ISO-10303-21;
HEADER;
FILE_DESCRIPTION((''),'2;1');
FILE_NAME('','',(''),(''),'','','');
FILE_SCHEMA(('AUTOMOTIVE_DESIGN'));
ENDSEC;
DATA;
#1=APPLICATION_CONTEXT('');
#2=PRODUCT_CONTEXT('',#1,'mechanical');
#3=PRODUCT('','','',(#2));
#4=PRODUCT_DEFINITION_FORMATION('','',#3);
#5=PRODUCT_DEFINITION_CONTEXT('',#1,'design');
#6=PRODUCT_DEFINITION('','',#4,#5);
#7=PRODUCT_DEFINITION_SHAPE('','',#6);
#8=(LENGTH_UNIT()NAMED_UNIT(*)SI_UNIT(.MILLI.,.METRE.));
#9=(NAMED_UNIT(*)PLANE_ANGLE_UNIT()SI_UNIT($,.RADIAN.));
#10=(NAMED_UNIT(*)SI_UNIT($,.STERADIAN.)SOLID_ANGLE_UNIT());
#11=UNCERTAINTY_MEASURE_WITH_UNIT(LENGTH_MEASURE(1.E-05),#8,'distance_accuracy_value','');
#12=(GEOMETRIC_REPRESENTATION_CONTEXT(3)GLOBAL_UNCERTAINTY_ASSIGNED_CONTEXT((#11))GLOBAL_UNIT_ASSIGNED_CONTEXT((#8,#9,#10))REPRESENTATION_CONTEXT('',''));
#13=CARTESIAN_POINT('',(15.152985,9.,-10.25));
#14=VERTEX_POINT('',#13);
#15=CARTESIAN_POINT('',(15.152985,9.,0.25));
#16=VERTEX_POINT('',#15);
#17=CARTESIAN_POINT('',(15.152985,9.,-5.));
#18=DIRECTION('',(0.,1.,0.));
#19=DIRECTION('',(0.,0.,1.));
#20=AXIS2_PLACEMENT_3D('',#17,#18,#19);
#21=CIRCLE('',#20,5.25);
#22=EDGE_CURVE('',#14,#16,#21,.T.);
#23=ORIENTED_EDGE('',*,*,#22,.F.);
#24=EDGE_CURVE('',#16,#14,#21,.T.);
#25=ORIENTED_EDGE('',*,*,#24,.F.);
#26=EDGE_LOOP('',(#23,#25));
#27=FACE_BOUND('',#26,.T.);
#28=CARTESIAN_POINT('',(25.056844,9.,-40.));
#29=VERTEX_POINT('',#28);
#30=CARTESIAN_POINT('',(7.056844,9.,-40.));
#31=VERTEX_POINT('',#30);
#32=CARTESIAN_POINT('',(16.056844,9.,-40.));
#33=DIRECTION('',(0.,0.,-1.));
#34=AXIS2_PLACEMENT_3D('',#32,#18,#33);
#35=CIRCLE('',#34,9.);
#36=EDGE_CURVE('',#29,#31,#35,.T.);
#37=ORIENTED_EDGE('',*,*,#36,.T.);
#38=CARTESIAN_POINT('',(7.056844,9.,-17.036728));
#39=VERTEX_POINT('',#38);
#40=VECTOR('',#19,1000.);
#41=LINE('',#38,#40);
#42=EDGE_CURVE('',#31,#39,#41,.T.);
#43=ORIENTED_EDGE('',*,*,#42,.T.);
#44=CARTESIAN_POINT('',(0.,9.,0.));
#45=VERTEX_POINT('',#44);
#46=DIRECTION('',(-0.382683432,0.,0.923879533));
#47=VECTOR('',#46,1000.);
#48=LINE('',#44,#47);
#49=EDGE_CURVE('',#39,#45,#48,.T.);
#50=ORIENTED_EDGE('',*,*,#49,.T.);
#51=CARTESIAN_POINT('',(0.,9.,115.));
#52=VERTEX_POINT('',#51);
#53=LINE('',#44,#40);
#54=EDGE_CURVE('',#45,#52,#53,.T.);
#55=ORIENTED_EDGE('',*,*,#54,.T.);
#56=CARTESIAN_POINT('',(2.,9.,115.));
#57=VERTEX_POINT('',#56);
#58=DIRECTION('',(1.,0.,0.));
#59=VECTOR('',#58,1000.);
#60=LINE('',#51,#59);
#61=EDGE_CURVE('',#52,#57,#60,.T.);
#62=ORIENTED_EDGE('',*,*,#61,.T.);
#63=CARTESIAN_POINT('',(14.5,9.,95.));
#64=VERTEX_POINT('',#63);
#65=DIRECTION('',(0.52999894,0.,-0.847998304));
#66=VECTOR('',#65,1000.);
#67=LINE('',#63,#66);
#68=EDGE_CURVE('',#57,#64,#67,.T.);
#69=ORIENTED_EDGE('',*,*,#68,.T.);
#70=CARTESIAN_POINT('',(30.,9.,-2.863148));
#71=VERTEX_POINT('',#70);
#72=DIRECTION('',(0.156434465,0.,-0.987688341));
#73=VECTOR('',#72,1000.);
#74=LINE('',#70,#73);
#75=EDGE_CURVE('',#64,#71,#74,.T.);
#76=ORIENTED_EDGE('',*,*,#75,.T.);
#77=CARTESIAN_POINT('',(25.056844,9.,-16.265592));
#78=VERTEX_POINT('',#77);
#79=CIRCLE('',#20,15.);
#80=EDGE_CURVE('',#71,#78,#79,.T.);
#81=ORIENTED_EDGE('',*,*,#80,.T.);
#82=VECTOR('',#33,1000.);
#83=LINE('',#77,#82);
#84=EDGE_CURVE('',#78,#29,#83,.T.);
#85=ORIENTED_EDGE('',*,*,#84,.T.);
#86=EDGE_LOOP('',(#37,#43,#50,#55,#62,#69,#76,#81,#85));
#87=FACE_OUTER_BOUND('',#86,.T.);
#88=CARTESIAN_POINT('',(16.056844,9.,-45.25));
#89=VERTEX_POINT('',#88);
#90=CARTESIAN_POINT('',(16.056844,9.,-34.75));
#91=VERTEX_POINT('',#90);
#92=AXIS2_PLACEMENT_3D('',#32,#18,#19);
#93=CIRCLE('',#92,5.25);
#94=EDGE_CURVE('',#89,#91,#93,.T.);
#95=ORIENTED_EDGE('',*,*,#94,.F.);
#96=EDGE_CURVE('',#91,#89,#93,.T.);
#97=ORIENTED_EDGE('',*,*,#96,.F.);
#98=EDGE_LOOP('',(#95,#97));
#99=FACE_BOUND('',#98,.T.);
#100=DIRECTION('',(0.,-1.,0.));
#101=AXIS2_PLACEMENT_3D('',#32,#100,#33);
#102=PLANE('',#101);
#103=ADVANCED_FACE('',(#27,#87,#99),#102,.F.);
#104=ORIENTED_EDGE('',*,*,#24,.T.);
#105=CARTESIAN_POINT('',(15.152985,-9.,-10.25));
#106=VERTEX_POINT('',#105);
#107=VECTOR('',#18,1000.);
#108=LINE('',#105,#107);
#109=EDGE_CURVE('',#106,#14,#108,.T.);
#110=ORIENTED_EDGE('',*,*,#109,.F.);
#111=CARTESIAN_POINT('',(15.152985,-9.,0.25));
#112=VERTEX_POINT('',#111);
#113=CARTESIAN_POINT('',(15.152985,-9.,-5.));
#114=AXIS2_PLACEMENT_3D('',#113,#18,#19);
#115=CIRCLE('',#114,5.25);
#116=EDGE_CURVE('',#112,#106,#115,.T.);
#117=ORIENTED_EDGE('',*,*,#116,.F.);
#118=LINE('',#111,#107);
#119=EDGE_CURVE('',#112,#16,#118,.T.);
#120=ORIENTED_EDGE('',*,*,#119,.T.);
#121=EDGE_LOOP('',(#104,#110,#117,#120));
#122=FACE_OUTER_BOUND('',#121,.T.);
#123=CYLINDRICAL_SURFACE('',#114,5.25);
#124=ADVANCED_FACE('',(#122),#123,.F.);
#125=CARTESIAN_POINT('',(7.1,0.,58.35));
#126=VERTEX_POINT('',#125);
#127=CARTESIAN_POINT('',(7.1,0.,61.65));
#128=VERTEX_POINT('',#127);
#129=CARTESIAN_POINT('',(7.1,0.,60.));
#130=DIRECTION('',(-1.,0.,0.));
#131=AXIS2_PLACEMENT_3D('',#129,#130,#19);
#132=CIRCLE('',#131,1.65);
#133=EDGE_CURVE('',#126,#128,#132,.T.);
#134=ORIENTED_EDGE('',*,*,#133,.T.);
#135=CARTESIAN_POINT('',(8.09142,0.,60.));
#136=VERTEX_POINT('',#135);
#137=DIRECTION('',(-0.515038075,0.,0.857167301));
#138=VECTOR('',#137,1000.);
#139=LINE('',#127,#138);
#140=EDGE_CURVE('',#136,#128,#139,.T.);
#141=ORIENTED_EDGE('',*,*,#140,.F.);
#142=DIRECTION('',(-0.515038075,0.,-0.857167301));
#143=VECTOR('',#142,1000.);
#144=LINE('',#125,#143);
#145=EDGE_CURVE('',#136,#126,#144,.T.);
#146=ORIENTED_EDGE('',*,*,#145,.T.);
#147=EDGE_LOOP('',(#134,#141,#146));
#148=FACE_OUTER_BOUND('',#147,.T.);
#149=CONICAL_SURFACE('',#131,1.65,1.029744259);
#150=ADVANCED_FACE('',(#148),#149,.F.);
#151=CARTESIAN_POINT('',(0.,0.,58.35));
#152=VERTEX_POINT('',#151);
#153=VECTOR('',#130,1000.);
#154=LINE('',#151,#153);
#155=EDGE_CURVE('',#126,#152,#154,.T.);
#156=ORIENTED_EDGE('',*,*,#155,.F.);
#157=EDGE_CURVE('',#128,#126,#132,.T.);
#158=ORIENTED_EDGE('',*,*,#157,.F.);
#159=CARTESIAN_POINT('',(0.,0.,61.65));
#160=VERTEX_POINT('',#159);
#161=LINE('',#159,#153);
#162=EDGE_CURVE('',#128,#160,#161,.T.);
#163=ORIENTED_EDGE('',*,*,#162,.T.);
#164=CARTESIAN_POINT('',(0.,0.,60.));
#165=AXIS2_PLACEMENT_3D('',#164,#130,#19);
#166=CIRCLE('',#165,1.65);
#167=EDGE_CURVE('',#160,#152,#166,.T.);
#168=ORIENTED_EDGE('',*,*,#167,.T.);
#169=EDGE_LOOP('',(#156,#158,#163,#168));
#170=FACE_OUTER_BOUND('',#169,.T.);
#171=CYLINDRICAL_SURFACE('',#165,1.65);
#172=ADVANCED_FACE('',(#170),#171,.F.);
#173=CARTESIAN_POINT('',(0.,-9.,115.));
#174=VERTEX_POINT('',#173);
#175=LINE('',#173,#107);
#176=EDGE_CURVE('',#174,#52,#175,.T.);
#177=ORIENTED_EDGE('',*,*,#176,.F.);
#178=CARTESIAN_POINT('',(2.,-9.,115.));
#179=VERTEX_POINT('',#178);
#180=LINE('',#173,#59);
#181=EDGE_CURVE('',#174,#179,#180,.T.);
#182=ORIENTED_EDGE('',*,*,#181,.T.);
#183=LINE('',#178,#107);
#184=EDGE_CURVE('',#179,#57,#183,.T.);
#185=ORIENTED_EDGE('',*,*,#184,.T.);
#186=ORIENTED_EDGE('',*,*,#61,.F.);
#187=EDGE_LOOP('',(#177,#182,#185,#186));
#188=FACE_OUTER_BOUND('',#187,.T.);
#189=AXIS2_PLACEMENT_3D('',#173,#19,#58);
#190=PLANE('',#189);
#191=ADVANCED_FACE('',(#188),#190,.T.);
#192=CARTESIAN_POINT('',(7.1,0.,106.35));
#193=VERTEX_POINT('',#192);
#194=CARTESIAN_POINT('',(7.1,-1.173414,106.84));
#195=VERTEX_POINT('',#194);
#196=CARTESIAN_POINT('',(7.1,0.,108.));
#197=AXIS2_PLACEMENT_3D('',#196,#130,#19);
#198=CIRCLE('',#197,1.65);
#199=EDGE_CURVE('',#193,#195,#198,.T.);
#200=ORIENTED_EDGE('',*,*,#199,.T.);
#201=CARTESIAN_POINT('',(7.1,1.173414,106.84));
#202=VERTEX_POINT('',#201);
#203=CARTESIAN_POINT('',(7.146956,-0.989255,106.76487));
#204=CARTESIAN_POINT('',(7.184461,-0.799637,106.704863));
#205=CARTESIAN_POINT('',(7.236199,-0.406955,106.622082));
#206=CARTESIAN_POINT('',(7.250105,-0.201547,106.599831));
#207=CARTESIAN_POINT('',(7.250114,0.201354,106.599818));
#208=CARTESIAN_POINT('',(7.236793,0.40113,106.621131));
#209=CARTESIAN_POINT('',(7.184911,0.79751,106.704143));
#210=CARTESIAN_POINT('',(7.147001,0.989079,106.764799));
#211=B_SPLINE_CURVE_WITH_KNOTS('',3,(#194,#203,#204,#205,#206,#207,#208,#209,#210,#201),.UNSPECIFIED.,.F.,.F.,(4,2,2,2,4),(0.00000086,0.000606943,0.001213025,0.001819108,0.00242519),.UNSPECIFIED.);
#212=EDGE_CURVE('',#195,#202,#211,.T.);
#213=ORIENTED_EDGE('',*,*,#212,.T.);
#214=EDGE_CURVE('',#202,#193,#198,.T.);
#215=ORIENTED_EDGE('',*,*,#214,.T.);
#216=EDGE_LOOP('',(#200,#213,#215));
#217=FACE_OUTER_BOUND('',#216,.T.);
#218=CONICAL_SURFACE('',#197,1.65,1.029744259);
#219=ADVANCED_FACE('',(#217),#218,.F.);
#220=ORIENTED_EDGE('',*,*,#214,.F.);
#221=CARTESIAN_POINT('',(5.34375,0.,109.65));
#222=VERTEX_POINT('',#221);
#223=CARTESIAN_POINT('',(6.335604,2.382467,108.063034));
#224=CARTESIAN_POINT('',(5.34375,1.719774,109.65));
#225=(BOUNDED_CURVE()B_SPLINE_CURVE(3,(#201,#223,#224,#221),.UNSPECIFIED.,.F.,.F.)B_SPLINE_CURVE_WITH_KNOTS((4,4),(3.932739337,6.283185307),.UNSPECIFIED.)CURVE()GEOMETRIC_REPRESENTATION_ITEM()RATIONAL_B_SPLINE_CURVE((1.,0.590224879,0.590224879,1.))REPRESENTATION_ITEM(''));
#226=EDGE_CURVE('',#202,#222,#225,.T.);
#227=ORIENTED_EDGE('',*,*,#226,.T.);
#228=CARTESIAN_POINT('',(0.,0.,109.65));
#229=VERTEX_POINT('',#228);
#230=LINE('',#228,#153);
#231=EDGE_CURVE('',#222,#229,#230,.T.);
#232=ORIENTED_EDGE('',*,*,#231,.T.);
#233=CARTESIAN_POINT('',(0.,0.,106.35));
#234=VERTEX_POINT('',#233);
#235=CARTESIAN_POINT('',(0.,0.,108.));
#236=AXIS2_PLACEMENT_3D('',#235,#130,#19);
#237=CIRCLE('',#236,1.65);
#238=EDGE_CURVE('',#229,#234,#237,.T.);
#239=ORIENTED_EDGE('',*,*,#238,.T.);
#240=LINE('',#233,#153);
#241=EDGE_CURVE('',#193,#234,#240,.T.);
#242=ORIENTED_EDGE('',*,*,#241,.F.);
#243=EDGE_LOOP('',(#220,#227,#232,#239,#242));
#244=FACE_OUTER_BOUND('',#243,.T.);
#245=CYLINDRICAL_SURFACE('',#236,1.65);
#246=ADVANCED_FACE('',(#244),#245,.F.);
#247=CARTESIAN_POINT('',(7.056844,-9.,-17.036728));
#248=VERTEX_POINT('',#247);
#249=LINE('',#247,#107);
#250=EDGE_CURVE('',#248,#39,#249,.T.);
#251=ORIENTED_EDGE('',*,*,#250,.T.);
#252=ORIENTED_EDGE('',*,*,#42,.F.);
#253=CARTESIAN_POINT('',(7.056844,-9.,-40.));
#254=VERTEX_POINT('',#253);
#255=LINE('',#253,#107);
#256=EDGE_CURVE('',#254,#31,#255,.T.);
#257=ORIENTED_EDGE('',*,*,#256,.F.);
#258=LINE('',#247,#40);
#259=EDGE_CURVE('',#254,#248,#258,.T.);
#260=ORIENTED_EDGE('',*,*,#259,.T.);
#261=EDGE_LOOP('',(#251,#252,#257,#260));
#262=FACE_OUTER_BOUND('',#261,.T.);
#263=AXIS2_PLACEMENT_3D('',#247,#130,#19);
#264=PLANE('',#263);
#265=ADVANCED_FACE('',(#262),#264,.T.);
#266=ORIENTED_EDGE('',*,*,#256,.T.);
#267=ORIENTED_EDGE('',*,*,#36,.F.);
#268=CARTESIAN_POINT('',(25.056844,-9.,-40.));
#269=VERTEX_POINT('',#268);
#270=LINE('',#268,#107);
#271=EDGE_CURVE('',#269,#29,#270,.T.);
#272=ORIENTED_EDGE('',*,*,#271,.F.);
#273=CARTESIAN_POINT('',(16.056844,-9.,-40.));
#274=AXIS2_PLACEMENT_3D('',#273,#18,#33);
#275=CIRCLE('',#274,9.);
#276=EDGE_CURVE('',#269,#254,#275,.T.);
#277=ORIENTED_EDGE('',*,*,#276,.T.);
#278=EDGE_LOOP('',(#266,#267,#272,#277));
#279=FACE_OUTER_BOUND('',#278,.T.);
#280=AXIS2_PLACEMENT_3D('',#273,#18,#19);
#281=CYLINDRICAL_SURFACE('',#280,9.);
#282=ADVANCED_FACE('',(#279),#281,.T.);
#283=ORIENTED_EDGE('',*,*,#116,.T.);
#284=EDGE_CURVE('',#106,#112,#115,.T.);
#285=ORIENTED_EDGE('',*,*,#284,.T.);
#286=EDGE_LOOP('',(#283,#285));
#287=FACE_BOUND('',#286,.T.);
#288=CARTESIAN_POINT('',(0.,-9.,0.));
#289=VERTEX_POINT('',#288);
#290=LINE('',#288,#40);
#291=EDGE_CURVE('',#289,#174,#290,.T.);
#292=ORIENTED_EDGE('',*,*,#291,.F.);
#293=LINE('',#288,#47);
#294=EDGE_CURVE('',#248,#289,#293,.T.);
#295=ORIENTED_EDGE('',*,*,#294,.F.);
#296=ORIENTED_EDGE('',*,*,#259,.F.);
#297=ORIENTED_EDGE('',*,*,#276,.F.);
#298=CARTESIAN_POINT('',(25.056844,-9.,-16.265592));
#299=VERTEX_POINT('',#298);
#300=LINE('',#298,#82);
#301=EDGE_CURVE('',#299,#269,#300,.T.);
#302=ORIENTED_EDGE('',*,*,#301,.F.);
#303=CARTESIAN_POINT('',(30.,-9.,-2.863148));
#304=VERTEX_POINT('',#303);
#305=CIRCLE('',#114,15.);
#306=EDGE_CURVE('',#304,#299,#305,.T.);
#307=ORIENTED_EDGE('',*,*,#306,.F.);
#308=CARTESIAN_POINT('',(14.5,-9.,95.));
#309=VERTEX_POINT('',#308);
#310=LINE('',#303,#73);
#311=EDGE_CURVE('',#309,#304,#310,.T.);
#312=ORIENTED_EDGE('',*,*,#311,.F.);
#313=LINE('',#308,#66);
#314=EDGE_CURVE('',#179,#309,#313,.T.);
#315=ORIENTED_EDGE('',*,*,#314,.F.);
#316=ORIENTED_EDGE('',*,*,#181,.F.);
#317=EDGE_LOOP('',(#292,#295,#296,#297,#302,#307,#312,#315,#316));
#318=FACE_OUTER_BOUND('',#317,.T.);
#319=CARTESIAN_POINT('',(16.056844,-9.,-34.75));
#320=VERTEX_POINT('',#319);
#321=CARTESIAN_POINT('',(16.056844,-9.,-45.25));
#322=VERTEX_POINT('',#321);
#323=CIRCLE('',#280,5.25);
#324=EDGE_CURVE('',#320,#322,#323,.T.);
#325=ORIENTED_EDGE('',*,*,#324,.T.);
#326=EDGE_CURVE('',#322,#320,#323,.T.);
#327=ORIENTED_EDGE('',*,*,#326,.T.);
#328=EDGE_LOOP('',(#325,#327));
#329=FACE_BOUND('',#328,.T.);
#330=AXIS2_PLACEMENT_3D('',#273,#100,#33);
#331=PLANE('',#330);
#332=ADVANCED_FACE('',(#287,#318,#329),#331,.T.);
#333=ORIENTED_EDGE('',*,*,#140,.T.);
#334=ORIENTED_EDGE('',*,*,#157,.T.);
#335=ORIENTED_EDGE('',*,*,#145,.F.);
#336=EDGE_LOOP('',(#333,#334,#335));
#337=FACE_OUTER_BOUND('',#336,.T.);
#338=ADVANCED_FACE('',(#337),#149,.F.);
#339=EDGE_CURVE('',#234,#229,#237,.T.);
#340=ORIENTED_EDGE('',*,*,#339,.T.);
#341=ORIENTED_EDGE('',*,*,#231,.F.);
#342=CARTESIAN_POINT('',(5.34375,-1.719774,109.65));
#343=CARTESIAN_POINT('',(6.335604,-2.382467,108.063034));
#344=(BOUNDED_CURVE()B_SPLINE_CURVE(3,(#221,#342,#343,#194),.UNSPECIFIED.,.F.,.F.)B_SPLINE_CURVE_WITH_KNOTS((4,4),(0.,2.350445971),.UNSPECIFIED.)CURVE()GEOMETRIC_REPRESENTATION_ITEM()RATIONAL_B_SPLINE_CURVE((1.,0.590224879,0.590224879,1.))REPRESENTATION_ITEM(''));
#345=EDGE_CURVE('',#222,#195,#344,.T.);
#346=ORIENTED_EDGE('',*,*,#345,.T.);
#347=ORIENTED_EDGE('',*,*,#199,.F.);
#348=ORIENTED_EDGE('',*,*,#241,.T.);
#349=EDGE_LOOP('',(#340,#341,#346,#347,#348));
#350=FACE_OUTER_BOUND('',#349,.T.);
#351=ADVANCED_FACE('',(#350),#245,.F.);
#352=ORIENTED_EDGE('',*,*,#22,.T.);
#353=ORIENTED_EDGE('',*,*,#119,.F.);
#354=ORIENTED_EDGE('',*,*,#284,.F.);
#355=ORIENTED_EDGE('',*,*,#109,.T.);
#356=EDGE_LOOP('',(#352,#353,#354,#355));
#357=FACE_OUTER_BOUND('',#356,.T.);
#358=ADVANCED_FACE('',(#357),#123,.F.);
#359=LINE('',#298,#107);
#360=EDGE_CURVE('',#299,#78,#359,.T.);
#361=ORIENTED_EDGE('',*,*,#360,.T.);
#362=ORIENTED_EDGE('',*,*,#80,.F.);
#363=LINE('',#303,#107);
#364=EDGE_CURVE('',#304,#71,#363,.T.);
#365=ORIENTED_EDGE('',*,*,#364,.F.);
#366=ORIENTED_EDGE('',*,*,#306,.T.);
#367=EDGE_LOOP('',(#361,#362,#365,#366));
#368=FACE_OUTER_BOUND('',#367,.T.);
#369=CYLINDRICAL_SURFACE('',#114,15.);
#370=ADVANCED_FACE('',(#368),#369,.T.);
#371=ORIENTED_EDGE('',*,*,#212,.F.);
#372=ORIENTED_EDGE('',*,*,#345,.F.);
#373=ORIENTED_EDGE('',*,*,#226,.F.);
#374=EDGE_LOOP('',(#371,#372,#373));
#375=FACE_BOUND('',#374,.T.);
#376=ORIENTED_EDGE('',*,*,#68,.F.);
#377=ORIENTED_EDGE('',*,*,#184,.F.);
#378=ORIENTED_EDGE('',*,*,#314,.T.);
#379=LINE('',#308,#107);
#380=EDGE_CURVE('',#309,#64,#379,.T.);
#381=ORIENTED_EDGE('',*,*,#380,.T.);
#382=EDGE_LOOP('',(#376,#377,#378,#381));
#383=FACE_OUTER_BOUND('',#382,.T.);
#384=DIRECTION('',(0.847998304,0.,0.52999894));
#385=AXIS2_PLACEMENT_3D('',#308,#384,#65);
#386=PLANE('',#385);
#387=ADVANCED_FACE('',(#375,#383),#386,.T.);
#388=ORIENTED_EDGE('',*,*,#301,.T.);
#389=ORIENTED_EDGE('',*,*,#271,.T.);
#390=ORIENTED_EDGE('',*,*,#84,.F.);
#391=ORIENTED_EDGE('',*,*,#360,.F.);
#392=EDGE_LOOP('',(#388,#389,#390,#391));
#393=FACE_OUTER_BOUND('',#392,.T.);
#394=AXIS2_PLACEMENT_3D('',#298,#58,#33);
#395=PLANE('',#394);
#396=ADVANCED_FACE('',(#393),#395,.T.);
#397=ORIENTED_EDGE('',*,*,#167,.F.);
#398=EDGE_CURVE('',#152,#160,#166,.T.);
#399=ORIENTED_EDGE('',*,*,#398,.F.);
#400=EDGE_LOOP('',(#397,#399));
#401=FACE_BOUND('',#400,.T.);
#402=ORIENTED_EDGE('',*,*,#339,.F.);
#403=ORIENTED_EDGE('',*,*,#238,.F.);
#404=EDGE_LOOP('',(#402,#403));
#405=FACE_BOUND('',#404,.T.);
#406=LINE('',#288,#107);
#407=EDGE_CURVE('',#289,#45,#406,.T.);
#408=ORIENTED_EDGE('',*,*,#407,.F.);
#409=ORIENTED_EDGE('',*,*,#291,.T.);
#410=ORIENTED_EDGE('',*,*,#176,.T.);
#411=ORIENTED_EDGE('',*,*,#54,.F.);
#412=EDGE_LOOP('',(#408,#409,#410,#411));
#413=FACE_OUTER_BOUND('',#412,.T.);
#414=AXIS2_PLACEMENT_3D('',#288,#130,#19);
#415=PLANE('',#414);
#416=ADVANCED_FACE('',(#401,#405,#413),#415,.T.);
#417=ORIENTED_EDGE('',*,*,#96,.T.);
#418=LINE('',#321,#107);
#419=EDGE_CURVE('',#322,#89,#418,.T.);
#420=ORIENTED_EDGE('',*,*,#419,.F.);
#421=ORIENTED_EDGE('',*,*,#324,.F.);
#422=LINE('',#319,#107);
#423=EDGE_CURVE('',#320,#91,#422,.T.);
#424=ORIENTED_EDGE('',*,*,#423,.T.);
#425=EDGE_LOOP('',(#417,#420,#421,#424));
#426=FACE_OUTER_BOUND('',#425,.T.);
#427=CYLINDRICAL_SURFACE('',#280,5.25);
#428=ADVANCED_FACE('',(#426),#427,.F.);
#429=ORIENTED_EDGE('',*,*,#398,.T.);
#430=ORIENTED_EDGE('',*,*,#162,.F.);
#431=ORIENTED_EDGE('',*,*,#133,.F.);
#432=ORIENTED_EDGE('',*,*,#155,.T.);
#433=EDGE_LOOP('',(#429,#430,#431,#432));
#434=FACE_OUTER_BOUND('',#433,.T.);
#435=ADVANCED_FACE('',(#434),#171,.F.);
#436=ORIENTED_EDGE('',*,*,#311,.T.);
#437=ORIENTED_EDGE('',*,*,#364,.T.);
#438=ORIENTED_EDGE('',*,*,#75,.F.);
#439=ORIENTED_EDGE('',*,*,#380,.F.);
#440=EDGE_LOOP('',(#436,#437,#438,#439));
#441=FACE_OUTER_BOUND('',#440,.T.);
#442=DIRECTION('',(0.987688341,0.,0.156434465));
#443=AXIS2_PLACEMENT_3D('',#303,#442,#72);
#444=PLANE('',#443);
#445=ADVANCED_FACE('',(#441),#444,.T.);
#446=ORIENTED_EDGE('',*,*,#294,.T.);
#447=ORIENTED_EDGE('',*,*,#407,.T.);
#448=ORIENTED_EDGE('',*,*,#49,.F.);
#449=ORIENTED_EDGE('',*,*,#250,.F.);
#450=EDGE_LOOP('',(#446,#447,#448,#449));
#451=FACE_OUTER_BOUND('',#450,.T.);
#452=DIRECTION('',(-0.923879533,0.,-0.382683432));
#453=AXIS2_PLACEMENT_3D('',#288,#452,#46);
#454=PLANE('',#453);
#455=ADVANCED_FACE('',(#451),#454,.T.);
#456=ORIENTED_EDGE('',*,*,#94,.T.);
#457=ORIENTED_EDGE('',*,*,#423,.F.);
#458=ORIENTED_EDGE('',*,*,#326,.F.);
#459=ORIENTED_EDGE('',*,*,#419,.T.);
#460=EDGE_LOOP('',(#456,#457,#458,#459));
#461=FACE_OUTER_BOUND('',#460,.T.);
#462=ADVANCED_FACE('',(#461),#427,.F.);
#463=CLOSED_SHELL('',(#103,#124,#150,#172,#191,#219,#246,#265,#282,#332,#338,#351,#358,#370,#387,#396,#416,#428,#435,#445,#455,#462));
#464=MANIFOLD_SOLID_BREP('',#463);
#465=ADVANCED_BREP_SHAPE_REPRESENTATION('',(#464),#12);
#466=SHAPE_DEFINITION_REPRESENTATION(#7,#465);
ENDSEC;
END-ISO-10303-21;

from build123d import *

# Parameters (mm, degrees)
BOSS_EXTRUDE1_DEPTH       = 9
BOSS_EXTRUDE1_DEPTH_BACK  = 9
SKETCH1_R                 = 5.25
M4X0_7_TAPPED_HOLE2_D     = 3.3
M4X0_7_TAPPED_HOLE2_DEPTH = 7.1
M4X0_7_TAPPED_HOLE2_TIP   = 0.991420021


with BuildPart() as part:
    # Sketch1 → Boss-Extrude1 (new, two sides: drawn at the far end of the back side and taken through both)
    with BuildSketch(Plane(origin=(0, 0, 0), x_dir=(1, 0, 0), z_dir=(0, 1, 0)).offset(-BOSS_EXTRUDE1_DEPTH_BACK)):
        with BuildLine():
            Line((0, 0), (0, -115))
            Line((0, -115), (2, -115))
            Line((2, -115), (14.5, -95))
            Line((14.5, -95), (30, 2.863148477))
            ThreePointArc((30, 2.863148477), (29.226286483, 10.190585207), (25.056843998, 16.265592284))
            Line((25.056843998, 16.265592284), (25.056843998, 40))
            ThreePointArc((25.056843998, 40), (16.056843998, 49), (7.056843998, 40))
            Line((7.056843998, 40), (7.056843998, 17.036728487))
            Line((7.056843998, 17.036728487), (0, 0))
        make_face()
        with Locations(Location((16.056843998, 40, 0), (0, 0, 270))):
            Circle(SKETCH1_R, mode=Mode.SUBTRACT)
        with Locations(Location((15.152984624, 5, 0), (0, 0, 270))):
            Circle(SKETCH1_R, mode=Mode.SUBTRACT)
    extrude(amount=BOSS_EXTRUDE1_DEPTH + BOSS_EXTRUDE1_DEPTH_BACK)

    # M4x0.7 Tapped Hole2
    with Locations(Plane(origin=(0, 0, 60), x_dir=(0, 0, -1), z_dir=(-1, 0, 0))):
        with Locations((0, 0), (-48, 0)):
            Hole(M4X0_7_TAPPED_HOLE2_D / 2, depth=M4X0_7_TAPPED_HOLE2_DEPTH)
            with Locations((0, 0, -(M4X0_7_TAPPED_HOLE2_DEPTH + M4X0_7_TAPPED_HOLE2_TIP / 2))):  # 118° drill point
                Cone(0, M4X0_7_TAPPED_HOLE2_D / 2, M4X0_7_TAPPED_HOLE2_TIP, mode=Mode.SUBTRACT)


solid = part.part
